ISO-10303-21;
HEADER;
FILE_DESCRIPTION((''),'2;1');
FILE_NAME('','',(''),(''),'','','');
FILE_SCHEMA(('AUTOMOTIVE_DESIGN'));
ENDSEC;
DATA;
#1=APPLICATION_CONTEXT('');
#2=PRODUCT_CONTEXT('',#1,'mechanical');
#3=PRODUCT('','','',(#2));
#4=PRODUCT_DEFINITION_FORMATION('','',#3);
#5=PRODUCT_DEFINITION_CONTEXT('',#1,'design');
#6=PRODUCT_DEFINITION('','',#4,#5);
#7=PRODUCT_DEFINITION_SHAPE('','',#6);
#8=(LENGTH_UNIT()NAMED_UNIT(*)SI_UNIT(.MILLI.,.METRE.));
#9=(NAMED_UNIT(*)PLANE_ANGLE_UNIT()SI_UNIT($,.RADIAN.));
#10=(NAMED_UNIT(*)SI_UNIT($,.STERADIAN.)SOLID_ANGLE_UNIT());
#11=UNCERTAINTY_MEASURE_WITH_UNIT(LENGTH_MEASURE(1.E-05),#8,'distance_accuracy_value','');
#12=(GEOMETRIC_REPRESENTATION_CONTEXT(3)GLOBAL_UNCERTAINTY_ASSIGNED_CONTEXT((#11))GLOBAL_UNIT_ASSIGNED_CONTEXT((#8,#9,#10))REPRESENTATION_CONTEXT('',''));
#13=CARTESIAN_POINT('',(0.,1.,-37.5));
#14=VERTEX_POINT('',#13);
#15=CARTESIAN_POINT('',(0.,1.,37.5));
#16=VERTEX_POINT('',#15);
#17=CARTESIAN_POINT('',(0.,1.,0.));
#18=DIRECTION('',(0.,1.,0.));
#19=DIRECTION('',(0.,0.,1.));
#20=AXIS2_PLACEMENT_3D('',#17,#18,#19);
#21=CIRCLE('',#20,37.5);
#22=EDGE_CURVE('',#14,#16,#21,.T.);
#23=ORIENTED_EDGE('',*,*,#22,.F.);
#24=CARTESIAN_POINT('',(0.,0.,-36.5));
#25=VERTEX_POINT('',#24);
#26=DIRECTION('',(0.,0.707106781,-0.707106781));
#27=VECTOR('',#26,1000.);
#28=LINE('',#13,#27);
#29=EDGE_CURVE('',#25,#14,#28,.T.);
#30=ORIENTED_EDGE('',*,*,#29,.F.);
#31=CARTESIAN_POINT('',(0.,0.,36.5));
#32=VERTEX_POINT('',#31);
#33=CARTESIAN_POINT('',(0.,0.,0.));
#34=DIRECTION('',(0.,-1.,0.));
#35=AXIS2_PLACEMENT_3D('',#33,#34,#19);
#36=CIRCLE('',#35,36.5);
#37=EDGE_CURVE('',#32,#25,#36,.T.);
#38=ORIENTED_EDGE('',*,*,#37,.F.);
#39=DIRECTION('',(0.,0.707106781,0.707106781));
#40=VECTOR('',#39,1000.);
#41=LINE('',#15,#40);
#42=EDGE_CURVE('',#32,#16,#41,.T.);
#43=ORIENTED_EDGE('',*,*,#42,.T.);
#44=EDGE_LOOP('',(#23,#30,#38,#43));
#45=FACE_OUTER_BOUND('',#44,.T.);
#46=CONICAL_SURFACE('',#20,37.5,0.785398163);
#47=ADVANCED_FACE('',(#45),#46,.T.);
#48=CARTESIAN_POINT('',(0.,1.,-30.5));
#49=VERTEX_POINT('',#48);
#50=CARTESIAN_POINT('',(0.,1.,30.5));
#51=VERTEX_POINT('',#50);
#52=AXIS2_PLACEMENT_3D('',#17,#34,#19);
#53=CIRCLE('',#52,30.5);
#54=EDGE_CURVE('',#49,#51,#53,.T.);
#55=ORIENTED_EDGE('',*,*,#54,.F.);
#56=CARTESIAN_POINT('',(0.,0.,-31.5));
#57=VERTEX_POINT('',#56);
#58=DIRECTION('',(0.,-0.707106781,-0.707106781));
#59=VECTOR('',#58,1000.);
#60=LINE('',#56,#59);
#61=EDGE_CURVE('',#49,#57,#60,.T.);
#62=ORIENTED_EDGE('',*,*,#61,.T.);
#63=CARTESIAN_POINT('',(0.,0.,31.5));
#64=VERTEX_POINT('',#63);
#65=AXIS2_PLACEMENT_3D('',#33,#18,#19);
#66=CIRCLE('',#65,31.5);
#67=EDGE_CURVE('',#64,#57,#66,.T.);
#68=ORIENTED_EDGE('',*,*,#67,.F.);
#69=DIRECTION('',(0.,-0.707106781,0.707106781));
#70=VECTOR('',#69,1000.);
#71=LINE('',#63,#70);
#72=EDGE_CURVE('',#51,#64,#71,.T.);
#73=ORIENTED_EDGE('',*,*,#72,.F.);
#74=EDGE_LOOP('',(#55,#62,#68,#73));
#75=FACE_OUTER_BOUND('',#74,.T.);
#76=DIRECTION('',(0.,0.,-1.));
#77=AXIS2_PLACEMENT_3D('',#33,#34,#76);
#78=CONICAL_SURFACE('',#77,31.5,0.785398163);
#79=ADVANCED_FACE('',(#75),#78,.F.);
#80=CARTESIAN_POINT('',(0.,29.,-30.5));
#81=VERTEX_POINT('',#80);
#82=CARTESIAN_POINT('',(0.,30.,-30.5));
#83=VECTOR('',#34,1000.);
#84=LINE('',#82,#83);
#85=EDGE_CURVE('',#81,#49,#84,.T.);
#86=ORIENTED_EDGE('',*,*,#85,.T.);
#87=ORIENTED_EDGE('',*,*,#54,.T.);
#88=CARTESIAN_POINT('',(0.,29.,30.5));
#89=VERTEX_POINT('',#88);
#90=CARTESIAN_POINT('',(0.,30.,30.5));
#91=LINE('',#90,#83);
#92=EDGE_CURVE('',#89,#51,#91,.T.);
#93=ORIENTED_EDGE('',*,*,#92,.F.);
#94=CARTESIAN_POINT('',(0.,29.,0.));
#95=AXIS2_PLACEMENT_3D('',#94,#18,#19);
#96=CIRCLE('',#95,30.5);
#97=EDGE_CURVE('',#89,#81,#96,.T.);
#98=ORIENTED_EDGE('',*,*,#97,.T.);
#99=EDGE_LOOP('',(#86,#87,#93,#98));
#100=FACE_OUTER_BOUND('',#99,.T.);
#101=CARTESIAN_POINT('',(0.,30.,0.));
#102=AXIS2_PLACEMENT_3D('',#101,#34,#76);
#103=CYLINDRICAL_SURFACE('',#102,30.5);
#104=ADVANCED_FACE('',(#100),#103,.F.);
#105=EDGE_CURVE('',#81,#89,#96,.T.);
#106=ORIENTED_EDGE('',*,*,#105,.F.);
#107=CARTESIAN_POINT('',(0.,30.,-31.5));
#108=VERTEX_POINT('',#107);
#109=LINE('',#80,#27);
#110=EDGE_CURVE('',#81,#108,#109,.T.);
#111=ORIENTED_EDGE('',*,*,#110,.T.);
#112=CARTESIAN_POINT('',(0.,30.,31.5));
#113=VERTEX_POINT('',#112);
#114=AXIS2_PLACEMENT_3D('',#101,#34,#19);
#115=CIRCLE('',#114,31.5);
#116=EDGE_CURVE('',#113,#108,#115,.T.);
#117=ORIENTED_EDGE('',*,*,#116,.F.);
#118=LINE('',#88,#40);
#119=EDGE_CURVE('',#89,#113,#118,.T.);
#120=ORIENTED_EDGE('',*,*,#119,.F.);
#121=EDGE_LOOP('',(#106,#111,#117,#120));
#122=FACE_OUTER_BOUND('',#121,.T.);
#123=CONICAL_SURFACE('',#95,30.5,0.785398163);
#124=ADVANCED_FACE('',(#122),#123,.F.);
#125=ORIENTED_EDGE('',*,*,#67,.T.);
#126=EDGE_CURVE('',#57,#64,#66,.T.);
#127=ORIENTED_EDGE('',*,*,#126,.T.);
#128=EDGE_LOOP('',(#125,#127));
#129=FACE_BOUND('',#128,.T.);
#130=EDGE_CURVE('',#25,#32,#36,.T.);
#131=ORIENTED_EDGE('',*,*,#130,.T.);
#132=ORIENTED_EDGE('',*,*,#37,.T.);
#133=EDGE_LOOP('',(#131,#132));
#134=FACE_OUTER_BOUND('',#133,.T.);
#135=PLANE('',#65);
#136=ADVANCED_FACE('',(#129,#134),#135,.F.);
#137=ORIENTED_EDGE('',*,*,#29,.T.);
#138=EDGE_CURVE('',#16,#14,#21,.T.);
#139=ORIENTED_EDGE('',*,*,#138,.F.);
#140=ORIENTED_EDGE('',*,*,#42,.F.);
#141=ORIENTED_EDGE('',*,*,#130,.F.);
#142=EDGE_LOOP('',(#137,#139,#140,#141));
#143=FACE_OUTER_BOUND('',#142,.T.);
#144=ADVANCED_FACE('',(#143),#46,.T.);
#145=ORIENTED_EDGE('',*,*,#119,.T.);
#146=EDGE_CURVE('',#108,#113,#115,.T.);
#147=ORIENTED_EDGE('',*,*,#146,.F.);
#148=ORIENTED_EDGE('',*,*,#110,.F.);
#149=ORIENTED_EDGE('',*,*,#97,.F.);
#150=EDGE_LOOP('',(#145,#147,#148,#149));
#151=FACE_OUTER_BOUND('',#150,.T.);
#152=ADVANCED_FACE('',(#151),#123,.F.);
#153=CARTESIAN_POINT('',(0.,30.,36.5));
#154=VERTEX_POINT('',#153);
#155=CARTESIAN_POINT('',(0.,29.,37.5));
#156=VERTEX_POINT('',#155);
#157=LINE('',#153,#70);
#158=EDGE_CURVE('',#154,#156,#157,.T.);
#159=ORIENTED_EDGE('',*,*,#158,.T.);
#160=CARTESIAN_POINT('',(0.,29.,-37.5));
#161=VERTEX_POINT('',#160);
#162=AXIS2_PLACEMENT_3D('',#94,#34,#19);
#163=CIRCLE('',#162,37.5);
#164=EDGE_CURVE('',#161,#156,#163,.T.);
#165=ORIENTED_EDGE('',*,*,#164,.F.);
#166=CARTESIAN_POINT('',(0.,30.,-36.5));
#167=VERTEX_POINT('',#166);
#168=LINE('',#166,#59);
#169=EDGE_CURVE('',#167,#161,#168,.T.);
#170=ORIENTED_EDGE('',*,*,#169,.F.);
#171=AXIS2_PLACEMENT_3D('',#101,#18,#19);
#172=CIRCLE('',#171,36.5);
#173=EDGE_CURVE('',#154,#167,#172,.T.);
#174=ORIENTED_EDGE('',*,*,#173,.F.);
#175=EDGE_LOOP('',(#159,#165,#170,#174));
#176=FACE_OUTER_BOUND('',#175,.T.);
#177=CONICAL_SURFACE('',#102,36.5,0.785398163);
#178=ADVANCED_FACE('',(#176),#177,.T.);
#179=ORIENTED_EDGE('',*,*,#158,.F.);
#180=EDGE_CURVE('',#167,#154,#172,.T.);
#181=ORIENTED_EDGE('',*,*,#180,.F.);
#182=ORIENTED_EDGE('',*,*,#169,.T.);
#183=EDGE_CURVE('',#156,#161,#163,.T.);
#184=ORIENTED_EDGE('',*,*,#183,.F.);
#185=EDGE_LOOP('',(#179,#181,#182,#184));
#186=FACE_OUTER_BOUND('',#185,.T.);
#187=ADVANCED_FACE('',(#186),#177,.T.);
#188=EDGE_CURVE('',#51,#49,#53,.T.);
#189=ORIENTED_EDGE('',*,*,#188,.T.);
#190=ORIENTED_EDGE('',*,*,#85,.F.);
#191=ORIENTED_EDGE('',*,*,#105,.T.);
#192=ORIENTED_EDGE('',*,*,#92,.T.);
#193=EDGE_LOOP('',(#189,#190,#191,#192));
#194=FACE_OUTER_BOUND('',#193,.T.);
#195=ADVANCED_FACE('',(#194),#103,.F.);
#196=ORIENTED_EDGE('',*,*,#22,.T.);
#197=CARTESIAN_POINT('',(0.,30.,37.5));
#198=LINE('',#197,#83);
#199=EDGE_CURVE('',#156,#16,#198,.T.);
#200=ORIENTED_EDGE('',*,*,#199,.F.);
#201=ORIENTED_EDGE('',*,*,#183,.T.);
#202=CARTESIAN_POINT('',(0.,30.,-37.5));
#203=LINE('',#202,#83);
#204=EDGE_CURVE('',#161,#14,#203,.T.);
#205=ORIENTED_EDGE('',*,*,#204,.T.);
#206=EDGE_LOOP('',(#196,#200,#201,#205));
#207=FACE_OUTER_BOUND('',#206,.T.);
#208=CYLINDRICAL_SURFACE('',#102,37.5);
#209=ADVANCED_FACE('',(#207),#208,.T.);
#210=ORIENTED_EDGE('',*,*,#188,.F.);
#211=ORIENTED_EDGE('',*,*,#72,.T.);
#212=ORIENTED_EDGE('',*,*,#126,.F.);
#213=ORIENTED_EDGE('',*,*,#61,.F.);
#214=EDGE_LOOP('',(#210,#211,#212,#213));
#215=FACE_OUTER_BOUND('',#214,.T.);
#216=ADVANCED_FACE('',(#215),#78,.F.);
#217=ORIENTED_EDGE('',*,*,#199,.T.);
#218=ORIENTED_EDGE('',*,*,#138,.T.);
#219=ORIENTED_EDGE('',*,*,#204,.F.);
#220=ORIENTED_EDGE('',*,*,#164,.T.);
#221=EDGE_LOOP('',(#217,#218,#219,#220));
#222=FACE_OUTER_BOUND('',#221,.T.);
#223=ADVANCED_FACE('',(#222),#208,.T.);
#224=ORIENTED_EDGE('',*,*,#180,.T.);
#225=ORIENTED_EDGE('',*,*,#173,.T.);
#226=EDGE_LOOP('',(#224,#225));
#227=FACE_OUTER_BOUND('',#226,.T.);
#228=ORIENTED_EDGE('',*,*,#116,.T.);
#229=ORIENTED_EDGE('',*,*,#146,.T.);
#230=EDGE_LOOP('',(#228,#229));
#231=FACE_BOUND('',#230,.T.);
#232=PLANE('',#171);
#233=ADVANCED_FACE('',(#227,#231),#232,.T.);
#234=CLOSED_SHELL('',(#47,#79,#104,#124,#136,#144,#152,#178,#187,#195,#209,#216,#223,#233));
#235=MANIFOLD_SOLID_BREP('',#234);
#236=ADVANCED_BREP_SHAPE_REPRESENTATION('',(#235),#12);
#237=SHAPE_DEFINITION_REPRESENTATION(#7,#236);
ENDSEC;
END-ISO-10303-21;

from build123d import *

# Parameters (mm, degrees)
SKETCH1_R           = 37.5
SKETCH1_R_2         = 30.5
BOSS_EXTRUDE1_DEPTH = 30
CHAMFER1_SIZE       = 1


with BuildPart() as part:
    # Sketch1 → Boss-Extrude1 (new body)
    with BuildSketch(Plane(origin=(0, 0, 0), x_dir=(1, 0, 0), z_dir=(0, 1, 0))):
        with Locations(Location((0, 0, 0), (0, 0, 270))):
            Circle(SKETCH1_R)
        with Locations(Location((0, 0, 0), (0, 0, 270))):
            Circle(SKETCH1_R_2, mode=Mode.SUBTRACT)
    extrude(amount=BOSS_EXTRUDE1_DEPTH)

    # Chamfer1
    chamfer1_edges = [part.edges().sort_by_distance(p)[0] for p in [
        (0, 0, -37.5),
        (0, 30, -37.5),
        (0, 0, -30.5),
        (0, 30, -30.5),
    ]]
    chamfer(chamfer1_edges, length=CHAMFER1_SIZE)


solid = part.part
